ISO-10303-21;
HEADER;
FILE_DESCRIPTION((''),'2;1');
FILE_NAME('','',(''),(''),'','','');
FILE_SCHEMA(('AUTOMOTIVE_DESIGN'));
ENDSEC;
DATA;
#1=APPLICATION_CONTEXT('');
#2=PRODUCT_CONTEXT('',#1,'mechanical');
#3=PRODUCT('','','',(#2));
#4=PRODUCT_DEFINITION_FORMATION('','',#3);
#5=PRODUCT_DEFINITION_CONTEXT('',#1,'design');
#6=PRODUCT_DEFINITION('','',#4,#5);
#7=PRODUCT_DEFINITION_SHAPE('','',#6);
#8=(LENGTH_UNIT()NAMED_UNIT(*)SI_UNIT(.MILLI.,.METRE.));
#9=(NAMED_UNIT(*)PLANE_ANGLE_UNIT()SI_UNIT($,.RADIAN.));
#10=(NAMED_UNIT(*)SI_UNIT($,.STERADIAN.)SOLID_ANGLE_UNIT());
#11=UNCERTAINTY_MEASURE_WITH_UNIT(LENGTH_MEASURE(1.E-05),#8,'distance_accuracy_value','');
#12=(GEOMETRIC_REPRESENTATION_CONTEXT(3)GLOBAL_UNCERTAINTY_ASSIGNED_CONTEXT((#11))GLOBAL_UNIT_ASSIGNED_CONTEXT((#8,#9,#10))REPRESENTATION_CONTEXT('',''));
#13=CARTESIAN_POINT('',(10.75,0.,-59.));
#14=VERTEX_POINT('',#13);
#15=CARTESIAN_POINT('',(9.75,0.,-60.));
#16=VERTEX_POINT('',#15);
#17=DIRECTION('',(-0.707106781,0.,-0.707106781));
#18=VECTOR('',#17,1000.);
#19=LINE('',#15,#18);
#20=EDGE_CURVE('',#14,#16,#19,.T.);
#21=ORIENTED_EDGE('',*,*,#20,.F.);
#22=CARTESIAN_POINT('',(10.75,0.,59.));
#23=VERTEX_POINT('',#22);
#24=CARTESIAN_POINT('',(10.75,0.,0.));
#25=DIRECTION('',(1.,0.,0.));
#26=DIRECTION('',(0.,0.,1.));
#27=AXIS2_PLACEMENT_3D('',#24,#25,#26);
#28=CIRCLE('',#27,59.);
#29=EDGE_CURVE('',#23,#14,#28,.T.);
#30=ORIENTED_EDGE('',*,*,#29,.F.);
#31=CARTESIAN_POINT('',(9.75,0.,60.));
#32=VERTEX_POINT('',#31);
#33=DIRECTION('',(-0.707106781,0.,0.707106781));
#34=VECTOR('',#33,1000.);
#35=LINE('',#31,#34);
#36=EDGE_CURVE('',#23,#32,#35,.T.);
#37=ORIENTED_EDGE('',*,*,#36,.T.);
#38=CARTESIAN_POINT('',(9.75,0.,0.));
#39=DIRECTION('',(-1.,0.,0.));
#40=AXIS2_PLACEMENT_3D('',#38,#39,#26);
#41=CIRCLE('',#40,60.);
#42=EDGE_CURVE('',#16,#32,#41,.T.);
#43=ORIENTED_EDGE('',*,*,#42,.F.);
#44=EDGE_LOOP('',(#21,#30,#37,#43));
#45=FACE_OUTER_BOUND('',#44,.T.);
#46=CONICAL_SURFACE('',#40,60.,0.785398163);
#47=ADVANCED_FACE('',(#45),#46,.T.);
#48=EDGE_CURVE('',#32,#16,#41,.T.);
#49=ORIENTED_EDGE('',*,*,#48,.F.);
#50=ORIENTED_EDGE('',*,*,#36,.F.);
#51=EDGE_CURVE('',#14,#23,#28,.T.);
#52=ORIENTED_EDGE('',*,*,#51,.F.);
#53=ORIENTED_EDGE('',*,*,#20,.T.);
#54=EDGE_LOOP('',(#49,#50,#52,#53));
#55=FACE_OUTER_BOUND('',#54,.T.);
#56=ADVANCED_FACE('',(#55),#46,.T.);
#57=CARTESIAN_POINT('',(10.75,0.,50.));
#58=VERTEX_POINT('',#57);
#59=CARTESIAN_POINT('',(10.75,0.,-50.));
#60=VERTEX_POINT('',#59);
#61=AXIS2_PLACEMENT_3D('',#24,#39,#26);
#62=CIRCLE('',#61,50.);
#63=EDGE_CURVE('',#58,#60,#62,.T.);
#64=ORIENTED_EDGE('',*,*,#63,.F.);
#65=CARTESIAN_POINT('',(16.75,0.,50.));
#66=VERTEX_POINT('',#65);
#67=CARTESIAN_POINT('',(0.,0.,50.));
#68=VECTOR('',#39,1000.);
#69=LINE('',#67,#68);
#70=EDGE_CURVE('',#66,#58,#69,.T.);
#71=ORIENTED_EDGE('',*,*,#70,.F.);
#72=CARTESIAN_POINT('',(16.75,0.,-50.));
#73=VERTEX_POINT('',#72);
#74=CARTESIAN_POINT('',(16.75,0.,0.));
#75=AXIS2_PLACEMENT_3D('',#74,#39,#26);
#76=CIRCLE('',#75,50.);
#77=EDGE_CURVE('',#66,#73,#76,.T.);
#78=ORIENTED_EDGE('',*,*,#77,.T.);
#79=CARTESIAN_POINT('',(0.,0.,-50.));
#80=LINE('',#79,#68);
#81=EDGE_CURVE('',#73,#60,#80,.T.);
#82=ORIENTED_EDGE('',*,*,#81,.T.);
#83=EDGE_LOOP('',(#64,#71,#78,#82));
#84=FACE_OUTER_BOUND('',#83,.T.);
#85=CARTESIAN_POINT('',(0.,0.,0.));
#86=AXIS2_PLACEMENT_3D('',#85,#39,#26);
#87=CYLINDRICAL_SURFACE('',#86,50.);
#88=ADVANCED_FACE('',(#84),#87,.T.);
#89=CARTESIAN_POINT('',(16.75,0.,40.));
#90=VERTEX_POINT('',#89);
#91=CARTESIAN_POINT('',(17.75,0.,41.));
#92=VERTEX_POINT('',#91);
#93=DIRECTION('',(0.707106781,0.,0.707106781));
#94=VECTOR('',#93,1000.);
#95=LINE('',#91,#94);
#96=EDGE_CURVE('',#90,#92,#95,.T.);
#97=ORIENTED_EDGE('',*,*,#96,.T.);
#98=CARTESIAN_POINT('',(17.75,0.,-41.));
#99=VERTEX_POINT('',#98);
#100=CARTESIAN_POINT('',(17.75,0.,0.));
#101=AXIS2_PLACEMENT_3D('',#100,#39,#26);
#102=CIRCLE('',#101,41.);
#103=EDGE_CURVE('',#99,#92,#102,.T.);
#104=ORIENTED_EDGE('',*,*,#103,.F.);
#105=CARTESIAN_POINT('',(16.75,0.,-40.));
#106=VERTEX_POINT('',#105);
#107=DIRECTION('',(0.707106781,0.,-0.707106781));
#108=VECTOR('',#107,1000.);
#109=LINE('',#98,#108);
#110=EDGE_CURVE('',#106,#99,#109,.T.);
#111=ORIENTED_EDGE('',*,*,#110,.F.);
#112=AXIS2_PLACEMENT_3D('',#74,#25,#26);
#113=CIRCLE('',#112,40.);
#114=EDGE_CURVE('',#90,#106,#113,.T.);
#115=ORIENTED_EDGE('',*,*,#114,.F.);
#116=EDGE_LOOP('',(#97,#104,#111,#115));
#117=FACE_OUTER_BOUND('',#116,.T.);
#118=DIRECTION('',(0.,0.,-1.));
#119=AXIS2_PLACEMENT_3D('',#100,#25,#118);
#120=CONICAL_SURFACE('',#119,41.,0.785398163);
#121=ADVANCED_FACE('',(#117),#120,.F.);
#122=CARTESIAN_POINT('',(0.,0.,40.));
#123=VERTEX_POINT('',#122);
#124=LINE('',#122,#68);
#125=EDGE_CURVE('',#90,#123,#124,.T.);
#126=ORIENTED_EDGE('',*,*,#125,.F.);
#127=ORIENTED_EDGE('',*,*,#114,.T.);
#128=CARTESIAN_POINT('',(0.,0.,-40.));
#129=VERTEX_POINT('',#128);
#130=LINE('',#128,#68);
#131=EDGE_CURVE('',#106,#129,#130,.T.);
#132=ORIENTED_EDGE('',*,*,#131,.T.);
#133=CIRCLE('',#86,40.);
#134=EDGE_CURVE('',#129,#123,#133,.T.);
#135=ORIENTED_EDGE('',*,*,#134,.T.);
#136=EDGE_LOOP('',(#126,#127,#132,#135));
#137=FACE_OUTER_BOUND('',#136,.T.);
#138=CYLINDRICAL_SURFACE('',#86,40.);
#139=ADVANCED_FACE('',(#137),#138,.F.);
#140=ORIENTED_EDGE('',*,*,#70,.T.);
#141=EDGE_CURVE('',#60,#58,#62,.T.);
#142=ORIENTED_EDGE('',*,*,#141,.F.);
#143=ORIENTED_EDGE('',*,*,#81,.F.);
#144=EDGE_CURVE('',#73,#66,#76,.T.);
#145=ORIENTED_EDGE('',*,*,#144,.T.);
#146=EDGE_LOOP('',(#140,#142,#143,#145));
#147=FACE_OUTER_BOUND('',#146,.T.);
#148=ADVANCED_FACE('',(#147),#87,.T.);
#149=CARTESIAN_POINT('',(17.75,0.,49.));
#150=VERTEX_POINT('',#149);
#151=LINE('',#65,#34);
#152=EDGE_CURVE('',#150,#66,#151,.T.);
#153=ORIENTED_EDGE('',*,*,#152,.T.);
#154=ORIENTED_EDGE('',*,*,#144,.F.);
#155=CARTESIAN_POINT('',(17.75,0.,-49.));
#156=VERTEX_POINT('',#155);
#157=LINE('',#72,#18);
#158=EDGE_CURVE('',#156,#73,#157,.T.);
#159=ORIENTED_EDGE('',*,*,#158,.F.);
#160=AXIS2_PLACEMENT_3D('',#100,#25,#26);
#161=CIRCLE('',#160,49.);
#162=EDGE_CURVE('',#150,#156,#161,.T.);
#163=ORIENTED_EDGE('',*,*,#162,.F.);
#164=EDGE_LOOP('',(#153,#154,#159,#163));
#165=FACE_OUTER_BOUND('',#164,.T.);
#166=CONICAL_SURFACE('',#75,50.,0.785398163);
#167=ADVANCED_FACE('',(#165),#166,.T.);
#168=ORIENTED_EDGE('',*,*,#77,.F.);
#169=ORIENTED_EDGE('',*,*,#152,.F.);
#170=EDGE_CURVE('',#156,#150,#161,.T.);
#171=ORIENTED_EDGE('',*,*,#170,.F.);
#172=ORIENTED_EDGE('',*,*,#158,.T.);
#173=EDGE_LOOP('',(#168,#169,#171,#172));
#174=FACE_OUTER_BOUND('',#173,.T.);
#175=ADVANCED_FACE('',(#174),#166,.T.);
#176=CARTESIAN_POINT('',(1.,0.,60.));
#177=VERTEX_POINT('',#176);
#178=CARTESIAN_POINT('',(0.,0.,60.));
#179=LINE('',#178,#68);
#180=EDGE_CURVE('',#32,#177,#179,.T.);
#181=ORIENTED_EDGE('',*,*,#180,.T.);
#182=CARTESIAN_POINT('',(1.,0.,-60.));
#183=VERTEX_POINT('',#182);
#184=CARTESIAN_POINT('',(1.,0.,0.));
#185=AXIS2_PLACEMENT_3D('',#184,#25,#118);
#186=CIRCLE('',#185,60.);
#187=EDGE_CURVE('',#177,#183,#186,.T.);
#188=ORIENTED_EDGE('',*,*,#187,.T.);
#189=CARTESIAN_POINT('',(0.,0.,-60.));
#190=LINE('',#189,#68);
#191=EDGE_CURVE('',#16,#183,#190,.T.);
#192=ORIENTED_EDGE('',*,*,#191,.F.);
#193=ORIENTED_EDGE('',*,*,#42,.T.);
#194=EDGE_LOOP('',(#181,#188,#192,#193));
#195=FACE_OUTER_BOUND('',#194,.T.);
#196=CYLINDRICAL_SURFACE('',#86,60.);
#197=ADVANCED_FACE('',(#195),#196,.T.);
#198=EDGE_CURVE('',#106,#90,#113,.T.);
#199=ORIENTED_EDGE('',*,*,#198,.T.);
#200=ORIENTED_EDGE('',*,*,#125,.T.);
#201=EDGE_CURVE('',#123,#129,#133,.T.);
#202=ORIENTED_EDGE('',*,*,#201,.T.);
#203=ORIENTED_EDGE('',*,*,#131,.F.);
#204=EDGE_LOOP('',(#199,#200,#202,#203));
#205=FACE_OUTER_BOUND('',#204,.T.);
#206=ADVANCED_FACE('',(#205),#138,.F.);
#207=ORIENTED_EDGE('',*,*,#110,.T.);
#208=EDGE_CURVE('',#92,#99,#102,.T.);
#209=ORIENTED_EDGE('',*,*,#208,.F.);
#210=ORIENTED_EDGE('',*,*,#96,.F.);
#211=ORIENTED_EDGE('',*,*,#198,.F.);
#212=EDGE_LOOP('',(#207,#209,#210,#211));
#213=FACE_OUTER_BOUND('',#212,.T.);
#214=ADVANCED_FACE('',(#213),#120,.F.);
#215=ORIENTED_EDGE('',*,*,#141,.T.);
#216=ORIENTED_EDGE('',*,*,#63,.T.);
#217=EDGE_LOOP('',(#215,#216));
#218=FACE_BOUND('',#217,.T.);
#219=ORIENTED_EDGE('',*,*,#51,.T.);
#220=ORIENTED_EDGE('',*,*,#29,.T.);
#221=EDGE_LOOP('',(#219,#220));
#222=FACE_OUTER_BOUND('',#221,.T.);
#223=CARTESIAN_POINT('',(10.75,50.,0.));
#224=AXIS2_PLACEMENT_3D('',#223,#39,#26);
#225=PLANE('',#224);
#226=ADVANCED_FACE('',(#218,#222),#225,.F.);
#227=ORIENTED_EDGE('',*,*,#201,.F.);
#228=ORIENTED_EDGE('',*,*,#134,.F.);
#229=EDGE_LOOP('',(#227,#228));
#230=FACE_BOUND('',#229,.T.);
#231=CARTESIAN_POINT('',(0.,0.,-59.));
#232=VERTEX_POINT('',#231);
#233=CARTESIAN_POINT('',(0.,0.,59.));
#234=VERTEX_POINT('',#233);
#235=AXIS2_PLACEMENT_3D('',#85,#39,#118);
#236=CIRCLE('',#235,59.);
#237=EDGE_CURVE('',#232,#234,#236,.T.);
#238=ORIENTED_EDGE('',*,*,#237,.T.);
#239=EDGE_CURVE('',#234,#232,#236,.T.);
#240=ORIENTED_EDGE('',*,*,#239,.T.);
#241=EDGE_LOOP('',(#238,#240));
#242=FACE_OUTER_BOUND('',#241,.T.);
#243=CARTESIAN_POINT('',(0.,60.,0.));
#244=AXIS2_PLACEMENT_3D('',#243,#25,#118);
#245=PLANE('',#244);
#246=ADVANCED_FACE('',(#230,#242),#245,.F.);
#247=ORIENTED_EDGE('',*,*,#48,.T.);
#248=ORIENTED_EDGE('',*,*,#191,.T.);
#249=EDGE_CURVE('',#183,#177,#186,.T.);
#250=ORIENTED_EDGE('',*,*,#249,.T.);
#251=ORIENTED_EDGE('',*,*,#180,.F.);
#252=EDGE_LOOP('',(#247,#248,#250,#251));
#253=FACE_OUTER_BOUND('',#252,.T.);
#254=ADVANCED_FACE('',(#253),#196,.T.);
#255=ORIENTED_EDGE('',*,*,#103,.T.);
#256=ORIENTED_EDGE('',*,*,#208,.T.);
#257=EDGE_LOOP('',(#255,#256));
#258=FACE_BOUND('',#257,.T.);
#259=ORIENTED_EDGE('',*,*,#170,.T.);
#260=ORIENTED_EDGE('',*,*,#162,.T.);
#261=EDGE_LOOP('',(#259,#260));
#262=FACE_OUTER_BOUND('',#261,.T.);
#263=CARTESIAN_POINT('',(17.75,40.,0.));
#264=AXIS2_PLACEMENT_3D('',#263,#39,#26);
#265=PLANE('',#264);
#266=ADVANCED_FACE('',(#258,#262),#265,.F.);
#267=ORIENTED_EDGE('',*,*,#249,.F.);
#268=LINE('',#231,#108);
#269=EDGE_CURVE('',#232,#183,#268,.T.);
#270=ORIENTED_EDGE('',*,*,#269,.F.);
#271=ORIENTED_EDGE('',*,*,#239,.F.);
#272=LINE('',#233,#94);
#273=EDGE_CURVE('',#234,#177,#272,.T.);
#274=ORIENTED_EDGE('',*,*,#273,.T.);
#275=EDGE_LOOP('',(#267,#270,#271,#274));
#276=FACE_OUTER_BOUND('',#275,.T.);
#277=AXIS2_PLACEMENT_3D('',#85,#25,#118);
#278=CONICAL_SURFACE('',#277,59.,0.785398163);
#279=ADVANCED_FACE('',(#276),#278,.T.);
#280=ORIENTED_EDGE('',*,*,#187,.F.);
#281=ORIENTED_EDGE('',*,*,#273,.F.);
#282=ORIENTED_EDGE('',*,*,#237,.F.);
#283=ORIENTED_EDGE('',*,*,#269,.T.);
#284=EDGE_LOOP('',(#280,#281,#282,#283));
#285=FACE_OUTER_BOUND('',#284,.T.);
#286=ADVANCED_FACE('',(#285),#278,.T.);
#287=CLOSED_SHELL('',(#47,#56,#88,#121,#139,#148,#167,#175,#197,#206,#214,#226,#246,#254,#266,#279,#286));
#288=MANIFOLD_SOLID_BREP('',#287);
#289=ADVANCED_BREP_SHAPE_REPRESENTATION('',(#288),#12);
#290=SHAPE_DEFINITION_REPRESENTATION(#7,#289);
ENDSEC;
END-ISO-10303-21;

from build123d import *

# Parameters (mm, degrees)
CHAMFER1_SIZE = 1


with BuildPart() as part:
    # Sketch1 → Revolve1 (revolve)
    with BuildSketch(Plane.XY, mode=Mode.PRIVATE) as revolve1_sk:
        Polygon((0, 60), (0, 40), (17.75, 40), (17.75, 50), (10.75, 50), (10.75, 60), align=None)
    revolve(revolve1_sk.sketch.rotate(Axis((0, 0, 0), (1, 0, 0)), 90), axis=Axis((0, 0, 0), (1, 0, 0)))

    # Chamfer1
    chamfer1_edges = [part.edges().sort_by_distance(p)[0] for p in [
        (10.75, 0, -60),
        (17.75, 0, -50),
        (17.75, 0, -40),
        (0, 0, -60),
    ]]
    chamfer(chamfer1_edges, length=CHAMFER1_SIZE)


solid = part.part
